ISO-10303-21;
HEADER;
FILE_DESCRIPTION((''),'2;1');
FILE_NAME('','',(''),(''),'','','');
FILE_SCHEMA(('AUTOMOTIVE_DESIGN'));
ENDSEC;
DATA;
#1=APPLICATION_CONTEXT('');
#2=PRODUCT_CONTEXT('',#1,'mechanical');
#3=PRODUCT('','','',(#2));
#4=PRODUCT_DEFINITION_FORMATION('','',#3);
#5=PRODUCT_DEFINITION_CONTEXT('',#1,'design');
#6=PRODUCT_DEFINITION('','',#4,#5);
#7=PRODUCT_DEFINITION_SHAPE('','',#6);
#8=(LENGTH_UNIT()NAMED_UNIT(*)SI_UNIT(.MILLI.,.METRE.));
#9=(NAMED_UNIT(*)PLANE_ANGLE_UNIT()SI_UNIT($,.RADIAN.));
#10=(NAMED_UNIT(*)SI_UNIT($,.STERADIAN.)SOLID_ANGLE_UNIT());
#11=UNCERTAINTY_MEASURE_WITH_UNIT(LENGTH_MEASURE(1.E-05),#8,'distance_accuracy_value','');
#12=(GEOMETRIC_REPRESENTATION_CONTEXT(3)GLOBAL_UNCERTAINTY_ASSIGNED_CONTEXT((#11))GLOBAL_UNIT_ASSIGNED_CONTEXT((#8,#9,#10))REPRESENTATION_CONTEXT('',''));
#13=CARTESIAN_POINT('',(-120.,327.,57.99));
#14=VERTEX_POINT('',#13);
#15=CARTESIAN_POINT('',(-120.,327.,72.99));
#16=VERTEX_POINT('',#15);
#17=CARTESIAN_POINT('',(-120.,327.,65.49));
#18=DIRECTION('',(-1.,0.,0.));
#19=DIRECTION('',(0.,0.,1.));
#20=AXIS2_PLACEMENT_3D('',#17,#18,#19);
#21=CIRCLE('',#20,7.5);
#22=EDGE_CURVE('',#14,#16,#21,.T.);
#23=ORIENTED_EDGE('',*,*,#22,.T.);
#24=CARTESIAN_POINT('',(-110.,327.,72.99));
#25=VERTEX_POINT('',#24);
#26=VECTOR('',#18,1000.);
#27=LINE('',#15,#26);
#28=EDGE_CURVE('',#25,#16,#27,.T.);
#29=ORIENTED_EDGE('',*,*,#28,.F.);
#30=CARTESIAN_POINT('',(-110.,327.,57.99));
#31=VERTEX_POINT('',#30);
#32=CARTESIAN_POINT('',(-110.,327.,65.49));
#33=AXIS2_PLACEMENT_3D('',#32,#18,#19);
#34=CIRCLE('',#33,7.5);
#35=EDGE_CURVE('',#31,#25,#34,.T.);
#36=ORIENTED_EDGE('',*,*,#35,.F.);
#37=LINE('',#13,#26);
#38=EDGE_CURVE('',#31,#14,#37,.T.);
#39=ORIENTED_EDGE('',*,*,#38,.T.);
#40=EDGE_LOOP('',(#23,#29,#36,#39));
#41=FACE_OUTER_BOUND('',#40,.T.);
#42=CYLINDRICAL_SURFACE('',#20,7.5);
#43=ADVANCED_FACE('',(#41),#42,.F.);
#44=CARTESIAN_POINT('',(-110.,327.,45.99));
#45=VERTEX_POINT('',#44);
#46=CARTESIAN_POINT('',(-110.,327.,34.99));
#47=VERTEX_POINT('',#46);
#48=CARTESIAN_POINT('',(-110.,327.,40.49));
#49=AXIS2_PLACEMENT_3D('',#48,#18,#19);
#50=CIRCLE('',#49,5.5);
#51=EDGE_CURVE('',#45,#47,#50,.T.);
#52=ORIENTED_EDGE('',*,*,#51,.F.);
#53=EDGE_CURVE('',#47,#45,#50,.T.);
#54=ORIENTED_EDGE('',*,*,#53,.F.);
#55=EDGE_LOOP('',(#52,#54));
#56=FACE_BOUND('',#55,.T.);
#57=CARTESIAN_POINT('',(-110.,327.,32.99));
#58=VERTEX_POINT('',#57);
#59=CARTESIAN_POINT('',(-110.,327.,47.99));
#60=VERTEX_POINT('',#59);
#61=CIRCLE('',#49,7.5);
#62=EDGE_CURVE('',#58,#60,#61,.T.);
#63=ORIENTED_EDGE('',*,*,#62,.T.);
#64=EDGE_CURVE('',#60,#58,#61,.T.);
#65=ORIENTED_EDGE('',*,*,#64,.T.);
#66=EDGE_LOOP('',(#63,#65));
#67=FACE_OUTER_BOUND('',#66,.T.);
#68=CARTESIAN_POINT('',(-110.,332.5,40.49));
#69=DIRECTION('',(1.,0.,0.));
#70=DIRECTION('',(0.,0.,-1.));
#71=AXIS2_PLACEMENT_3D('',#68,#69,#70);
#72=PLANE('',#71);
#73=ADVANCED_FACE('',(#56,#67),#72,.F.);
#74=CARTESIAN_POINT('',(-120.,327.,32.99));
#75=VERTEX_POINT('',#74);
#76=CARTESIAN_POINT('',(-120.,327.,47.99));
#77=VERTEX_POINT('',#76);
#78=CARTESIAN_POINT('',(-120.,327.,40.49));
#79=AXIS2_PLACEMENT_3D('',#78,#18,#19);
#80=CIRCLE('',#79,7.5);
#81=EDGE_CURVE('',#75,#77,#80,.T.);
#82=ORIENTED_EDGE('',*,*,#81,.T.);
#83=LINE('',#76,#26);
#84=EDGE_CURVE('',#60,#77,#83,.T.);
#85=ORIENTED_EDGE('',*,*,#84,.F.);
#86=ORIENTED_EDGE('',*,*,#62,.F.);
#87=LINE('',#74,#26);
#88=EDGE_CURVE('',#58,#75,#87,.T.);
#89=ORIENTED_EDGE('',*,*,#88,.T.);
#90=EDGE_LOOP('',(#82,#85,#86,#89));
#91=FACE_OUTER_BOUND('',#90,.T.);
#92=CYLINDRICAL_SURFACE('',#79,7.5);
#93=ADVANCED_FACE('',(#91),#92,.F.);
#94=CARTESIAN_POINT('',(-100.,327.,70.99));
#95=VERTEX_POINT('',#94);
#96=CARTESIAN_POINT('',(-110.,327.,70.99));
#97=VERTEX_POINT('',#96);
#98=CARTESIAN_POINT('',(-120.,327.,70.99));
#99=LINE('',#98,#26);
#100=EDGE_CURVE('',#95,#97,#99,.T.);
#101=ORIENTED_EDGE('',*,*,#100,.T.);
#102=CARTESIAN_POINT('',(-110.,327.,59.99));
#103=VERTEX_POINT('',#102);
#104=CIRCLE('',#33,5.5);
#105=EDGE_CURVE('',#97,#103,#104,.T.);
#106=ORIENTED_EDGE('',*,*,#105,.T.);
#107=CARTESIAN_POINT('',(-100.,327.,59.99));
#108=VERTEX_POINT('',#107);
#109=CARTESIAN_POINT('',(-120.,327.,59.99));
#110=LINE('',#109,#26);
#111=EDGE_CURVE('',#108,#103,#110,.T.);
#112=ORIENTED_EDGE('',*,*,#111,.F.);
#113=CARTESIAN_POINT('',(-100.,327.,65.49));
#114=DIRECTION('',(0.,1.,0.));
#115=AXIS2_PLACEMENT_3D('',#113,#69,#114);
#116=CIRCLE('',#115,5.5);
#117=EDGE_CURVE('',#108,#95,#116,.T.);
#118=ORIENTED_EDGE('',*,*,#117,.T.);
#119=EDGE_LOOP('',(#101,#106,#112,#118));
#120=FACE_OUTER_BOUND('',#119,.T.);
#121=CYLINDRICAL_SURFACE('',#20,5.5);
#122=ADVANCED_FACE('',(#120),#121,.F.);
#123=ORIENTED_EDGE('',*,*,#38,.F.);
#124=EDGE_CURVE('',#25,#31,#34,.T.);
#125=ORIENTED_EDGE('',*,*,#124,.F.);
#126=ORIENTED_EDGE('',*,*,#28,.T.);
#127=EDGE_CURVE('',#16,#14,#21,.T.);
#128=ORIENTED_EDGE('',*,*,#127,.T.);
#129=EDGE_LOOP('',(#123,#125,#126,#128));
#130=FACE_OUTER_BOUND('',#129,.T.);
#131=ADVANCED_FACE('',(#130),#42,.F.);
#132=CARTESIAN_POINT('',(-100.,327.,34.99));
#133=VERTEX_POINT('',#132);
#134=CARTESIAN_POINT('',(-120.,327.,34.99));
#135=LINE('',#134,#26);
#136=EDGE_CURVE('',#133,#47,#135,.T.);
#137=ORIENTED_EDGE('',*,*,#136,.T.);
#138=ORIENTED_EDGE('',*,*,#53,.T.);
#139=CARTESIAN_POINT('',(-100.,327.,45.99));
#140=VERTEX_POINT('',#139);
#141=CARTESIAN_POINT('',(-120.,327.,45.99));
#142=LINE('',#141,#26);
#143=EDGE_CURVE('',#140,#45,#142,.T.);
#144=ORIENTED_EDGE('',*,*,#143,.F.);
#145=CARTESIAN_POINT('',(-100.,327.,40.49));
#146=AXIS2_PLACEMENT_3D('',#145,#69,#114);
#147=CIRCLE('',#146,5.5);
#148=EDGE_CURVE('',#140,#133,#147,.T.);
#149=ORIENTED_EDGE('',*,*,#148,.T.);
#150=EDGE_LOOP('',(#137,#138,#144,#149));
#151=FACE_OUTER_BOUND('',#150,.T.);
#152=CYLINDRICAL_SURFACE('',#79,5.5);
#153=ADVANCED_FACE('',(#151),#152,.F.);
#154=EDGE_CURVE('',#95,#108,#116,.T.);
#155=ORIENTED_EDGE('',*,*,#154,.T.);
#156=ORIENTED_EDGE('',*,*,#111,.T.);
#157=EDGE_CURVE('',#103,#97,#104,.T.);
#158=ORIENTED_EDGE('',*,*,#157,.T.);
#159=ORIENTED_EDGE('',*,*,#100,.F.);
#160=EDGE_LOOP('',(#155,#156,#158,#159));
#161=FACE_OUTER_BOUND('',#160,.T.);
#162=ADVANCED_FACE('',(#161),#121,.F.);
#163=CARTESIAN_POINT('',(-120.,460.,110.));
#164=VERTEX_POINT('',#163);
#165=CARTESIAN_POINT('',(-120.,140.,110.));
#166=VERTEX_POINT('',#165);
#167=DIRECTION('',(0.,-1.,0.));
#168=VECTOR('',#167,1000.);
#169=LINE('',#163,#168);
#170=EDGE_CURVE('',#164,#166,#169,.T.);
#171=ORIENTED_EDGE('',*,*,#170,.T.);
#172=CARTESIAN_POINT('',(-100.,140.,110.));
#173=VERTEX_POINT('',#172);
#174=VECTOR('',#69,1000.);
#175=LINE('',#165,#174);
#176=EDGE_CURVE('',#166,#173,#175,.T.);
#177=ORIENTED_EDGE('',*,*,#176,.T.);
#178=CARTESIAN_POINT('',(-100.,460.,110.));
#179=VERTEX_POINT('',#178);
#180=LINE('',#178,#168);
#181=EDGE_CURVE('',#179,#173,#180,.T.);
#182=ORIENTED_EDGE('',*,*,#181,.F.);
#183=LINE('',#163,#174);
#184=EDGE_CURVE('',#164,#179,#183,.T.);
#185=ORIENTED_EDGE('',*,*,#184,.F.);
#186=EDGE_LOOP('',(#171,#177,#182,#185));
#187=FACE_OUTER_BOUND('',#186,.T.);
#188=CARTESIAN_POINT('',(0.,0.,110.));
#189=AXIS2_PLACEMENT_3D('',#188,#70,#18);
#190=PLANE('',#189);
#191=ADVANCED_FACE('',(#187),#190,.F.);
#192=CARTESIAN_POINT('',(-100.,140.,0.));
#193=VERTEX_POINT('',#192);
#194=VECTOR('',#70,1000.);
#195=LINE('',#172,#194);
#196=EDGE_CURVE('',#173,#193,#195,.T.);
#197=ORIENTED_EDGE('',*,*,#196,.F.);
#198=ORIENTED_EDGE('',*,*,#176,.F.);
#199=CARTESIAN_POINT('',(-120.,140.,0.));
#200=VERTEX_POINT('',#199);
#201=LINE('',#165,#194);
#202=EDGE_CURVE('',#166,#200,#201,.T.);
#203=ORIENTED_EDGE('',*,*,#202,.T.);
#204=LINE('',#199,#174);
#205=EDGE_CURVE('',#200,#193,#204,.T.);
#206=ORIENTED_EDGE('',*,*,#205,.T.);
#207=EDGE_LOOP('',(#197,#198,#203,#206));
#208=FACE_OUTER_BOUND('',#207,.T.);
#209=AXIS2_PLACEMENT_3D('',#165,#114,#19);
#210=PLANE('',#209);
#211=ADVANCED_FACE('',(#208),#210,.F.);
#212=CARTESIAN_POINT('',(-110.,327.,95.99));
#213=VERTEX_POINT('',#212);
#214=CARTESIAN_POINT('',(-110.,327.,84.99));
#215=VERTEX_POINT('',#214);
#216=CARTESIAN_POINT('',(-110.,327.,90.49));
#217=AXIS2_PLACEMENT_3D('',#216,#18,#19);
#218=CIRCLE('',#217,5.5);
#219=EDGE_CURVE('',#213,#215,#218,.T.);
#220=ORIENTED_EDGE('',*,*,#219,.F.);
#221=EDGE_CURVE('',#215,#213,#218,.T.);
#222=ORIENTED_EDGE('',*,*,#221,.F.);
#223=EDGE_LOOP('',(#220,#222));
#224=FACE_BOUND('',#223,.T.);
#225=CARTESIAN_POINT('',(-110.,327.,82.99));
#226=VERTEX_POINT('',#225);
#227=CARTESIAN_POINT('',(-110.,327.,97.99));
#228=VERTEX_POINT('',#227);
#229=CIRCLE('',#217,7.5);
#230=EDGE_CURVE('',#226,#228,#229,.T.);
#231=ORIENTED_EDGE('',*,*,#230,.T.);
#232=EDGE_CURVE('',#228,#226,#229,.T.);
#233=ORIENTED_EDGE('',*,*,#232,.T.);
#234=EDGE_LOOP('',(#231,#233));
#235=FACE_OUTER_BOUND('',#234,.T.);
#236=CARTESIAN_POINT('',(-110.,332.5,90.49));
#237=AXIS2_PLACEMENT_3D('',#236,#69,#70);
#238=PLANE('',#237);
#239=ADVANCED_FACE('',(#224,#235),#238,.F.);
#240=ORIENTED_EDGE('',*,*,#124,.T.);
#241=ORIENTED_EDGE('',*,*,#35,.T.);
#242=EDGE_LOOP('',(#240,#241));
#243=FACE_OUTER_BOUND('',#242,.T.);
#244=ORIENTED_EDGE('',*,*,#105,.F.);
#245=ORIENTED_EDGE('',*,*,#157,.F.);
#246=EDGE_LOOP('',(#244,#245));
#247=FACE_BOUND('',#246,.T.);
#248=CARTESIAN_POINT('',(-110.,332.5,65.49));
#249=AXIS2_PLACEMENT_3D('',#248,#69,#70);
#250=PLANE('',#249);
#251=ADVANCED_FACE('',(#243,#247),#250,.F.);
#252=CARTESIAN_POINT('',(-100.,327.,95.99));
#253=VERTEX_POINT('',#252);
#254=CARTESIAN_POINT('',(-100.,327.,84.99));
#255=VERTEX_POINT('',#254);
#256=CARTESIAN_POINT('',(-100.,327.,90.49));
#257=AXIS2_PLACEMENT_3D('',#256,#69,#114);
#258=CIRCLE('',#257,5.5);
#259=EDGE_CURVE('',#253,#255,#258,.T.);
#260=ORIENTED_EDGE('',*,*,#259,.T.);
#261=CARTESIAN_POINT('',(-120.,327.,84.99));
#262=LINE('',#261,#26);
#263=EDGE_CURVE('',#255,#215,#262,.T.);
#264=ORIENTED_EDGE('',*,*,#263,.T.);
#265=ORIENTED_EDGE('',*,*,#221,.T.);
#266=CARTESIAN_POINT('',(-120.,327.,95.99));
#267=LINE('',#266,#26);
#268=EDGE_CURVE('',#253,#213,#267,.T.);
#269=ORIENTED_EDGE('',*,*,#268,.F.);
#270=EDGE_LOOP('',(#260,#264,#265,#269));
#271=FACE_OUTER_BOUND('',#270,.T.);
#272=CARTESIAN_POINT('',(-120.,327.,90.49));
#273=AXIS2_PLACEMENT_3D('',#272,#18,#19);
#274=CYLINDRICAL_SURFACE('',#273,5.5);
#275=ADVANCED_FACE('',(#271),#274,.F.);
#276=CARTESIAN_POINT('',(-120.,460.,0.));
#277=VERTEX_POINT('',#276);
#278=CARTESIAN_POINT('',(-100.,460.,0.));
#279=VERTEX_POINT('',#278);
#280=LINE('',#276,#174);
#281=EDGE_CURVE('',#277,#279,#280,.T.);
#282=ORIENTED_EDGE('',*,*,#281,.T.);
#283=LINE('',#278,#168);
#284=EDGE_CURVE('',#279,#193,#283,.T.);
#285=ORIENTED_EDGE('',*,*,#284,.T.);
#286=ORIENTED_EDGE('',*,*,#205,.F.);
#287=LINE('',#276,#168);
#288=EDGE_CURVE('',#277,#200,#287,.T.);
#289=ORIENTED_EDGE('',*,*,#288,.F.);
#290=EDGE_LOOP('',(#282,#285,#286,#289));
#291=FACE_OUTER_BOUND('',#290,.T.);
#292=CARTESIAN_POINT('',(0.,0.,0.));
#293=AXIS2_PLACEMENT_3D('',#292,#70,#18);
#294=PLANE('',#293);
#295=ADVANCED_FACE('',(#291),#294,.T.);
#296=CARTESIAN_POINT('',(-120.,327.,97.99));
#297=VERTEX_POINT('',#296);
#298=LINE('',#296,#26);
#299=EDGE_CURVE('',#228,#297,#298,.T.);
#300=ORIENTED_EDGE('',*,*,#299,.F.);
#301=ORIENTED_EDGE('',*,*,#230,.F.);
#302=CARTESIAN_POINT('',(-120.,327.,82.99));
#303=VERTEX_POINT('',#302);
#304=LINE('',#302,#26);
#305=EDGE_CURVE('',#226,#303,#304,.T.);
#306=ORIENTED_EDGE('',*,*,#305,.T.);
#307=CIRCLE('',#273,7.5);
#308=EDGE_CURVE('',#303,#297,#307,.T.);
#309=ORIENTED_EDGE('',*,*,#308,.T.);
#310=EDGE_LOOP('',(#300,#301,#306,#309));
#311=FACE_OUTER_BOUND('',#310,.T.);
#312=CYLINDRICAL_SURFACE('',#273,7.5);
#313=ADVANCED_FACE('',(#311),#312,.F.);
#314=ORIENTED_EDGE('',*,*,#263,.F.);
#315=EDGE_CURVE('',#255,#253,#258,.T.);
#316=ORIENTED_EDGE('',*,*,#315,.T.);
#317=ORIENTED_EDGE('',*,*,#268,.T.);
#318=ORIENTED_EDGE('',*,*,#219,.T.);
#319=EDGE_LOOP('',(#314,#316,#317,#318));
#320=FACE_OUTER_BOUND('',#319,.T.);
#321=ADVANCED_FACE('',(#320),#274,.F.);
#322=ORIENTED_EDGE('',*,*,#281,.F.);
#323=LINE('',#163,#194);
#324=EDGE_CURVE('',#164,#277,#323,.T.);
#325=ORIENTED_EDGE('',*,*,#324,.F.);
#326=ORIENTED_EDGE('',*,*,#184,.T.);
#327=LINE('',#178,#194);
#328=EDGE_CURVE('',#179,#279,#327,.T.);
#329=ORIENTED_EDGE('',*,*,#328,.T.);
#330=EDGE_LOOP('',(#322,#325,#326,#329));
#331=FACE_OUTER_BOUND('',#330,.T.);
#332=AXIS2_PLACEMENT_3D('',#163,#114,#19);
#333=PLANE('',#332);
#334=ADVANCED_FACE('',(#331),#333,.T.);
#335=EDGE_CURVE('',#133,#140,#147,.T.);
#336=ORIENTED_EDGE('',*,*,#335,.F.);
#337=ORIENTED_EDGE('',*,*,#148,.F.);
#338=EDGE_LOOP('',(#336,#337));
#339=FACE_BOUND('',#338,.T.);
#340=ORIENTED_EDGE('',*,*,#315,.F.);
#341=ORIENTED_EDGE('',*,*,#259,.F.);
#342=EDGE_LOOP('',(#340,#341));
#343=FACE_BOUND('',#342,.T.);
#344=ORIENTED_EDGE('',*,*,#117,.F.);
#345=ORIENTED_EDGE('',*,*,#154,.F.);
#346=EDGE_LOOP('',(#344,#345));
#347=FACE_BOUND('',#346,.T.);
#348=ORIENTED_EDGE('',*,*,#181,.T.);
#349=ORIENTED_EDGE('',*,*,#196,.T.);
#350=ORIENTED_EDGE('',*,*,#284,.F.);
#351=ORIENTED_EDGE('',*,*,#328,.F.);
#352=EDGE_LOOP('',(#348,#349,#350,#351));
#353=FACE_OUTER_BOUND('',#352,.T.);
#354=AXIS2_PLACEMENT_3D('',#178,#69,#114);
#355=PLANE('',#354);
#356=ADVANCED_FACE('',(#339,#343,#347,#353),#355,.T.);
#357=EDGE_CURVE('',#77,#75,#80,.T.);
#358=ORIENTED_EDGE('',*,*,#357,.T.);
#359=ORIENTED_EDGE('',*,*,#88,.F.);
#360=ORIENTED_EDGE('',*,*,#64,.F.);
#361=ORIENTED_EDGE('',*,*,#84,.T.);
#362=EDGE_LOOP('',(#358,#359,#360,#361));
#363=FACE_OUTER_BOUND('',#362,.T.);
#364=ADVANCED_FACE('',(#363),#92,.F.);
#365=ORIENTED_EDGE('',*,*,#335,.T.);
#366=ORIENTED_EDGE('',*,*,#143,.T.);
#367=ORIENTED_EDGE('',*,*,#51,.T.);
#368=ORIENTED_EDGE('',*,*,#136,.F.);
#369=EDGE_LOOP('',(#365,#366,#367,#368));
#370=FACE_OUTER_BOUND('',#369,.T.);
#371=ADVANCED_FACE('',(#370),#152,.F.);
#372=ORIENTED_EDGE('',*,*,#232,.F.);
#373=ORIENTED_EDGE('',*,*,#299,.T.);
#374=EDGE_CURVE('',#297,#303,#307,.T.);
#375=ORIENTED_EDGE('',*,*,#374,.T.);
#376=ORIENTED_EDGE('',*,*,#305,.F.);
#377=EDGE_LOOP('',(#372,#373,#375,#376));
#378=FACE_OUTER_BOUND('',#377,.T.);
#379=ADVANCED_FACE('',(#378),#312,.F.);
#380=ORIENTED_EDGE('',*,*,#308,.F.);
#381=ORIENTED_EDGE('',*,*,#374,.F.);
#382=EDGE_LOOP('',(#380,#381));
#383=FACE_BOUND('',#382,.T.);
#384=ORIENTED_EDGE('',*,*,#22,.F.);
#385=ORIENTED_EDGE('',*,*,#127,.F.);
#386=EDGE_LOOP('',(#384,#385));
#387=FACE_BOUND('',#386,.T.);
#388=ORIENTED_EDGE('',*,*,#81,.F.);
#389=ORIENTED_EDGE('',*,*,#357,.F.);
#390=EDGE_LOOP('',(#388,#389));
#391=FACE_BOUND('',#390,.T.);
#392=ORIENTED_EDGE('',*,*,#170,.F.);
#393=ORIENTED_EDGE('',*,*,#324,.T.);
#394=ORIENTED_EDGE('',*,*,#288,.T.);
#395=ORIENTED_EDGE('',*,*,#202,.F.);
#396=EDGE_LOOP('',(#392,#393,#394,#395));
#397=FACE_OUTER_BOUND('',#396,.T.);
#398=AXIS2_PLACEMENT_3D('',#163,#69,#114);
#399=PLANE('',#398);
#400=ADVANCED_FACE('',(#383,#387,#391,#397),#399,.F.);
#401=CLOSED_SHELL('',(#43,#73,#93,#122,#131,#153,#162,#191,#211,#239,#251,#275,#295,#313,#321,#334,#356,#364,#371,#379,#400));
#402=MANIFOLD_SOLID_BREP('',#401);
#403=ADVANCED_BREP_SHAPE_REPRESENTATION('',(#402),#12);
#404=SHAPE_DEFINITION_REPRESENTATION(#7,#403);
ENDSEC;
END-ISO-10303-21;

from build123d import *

# Parameters (mm, degrees)
SKETCH1_W                                = 20
SKETCH1_H                                = 320
BOSS_EXTRUDE1_DEPTH                      = 110
CBORE_FOR_M10_HEX_HEAD_BOLT1_D           = 11
CBORE_FOR_M10_HEX_HEAD_BOLT1_DEPTH       = 22.25
CBORE_FOR_M10_HEX_HEAD_BOLT1_CBORE_D     = 15
CBORE_FOR_M10_HEX_HEAD_BOLT1_CBORE_DEPTH = 10
CBORE_FOR_M10_HEX_HEAD_BOLT1_TIP         = 3.304733405


with BuildPart() as part:
    # Sketch1 → Boss-Extrude1 (new body)
    with BuildSketch(Plane.XY):
        with Locations((-110, 300)):
            Rectangle(SKETCH1_W, SKETCH1_H)
    extrude(amount=BOSS_EXTRUDE1_DEPTH)

    # CBORE for M10 Hex Head Bolt1
    with Locations(Plane.ZY.offset(120)):
        with Locations((40.49, 327), (65.49, 327), (90.49, 327)):
            CounterBoreHole(CBORE_FOR_M10_HEX_HEAD_BOLT1_D / 2, CBORE_FOR_M10_HEX_HEAD_BOLT1_CBORE_D / 2, CBORE_FOR_M10_HEX_HEAD_BOLT1_CBORE_DEPTH, depth=CBORE_FOR_M10_HEX_HEAD_BOLT1_DEPTH)
            with Locations((0, 0, -(CBORE_FOR_M10_HEX_HEAD_BOLT1_DEPTH + CBORE_FOR_M10_HEX_HEAD_BOLT1_TIP / 2))):  # 118° drill point
                Cone(0, CBORE_FOR_M10_HEX_HEAD_BOLT1_D / 2, CBORE_FOR_M10_HEX_HEAD_BOLT1_TIP, mode=Mode.SUBTRACT)


solid = part.part
